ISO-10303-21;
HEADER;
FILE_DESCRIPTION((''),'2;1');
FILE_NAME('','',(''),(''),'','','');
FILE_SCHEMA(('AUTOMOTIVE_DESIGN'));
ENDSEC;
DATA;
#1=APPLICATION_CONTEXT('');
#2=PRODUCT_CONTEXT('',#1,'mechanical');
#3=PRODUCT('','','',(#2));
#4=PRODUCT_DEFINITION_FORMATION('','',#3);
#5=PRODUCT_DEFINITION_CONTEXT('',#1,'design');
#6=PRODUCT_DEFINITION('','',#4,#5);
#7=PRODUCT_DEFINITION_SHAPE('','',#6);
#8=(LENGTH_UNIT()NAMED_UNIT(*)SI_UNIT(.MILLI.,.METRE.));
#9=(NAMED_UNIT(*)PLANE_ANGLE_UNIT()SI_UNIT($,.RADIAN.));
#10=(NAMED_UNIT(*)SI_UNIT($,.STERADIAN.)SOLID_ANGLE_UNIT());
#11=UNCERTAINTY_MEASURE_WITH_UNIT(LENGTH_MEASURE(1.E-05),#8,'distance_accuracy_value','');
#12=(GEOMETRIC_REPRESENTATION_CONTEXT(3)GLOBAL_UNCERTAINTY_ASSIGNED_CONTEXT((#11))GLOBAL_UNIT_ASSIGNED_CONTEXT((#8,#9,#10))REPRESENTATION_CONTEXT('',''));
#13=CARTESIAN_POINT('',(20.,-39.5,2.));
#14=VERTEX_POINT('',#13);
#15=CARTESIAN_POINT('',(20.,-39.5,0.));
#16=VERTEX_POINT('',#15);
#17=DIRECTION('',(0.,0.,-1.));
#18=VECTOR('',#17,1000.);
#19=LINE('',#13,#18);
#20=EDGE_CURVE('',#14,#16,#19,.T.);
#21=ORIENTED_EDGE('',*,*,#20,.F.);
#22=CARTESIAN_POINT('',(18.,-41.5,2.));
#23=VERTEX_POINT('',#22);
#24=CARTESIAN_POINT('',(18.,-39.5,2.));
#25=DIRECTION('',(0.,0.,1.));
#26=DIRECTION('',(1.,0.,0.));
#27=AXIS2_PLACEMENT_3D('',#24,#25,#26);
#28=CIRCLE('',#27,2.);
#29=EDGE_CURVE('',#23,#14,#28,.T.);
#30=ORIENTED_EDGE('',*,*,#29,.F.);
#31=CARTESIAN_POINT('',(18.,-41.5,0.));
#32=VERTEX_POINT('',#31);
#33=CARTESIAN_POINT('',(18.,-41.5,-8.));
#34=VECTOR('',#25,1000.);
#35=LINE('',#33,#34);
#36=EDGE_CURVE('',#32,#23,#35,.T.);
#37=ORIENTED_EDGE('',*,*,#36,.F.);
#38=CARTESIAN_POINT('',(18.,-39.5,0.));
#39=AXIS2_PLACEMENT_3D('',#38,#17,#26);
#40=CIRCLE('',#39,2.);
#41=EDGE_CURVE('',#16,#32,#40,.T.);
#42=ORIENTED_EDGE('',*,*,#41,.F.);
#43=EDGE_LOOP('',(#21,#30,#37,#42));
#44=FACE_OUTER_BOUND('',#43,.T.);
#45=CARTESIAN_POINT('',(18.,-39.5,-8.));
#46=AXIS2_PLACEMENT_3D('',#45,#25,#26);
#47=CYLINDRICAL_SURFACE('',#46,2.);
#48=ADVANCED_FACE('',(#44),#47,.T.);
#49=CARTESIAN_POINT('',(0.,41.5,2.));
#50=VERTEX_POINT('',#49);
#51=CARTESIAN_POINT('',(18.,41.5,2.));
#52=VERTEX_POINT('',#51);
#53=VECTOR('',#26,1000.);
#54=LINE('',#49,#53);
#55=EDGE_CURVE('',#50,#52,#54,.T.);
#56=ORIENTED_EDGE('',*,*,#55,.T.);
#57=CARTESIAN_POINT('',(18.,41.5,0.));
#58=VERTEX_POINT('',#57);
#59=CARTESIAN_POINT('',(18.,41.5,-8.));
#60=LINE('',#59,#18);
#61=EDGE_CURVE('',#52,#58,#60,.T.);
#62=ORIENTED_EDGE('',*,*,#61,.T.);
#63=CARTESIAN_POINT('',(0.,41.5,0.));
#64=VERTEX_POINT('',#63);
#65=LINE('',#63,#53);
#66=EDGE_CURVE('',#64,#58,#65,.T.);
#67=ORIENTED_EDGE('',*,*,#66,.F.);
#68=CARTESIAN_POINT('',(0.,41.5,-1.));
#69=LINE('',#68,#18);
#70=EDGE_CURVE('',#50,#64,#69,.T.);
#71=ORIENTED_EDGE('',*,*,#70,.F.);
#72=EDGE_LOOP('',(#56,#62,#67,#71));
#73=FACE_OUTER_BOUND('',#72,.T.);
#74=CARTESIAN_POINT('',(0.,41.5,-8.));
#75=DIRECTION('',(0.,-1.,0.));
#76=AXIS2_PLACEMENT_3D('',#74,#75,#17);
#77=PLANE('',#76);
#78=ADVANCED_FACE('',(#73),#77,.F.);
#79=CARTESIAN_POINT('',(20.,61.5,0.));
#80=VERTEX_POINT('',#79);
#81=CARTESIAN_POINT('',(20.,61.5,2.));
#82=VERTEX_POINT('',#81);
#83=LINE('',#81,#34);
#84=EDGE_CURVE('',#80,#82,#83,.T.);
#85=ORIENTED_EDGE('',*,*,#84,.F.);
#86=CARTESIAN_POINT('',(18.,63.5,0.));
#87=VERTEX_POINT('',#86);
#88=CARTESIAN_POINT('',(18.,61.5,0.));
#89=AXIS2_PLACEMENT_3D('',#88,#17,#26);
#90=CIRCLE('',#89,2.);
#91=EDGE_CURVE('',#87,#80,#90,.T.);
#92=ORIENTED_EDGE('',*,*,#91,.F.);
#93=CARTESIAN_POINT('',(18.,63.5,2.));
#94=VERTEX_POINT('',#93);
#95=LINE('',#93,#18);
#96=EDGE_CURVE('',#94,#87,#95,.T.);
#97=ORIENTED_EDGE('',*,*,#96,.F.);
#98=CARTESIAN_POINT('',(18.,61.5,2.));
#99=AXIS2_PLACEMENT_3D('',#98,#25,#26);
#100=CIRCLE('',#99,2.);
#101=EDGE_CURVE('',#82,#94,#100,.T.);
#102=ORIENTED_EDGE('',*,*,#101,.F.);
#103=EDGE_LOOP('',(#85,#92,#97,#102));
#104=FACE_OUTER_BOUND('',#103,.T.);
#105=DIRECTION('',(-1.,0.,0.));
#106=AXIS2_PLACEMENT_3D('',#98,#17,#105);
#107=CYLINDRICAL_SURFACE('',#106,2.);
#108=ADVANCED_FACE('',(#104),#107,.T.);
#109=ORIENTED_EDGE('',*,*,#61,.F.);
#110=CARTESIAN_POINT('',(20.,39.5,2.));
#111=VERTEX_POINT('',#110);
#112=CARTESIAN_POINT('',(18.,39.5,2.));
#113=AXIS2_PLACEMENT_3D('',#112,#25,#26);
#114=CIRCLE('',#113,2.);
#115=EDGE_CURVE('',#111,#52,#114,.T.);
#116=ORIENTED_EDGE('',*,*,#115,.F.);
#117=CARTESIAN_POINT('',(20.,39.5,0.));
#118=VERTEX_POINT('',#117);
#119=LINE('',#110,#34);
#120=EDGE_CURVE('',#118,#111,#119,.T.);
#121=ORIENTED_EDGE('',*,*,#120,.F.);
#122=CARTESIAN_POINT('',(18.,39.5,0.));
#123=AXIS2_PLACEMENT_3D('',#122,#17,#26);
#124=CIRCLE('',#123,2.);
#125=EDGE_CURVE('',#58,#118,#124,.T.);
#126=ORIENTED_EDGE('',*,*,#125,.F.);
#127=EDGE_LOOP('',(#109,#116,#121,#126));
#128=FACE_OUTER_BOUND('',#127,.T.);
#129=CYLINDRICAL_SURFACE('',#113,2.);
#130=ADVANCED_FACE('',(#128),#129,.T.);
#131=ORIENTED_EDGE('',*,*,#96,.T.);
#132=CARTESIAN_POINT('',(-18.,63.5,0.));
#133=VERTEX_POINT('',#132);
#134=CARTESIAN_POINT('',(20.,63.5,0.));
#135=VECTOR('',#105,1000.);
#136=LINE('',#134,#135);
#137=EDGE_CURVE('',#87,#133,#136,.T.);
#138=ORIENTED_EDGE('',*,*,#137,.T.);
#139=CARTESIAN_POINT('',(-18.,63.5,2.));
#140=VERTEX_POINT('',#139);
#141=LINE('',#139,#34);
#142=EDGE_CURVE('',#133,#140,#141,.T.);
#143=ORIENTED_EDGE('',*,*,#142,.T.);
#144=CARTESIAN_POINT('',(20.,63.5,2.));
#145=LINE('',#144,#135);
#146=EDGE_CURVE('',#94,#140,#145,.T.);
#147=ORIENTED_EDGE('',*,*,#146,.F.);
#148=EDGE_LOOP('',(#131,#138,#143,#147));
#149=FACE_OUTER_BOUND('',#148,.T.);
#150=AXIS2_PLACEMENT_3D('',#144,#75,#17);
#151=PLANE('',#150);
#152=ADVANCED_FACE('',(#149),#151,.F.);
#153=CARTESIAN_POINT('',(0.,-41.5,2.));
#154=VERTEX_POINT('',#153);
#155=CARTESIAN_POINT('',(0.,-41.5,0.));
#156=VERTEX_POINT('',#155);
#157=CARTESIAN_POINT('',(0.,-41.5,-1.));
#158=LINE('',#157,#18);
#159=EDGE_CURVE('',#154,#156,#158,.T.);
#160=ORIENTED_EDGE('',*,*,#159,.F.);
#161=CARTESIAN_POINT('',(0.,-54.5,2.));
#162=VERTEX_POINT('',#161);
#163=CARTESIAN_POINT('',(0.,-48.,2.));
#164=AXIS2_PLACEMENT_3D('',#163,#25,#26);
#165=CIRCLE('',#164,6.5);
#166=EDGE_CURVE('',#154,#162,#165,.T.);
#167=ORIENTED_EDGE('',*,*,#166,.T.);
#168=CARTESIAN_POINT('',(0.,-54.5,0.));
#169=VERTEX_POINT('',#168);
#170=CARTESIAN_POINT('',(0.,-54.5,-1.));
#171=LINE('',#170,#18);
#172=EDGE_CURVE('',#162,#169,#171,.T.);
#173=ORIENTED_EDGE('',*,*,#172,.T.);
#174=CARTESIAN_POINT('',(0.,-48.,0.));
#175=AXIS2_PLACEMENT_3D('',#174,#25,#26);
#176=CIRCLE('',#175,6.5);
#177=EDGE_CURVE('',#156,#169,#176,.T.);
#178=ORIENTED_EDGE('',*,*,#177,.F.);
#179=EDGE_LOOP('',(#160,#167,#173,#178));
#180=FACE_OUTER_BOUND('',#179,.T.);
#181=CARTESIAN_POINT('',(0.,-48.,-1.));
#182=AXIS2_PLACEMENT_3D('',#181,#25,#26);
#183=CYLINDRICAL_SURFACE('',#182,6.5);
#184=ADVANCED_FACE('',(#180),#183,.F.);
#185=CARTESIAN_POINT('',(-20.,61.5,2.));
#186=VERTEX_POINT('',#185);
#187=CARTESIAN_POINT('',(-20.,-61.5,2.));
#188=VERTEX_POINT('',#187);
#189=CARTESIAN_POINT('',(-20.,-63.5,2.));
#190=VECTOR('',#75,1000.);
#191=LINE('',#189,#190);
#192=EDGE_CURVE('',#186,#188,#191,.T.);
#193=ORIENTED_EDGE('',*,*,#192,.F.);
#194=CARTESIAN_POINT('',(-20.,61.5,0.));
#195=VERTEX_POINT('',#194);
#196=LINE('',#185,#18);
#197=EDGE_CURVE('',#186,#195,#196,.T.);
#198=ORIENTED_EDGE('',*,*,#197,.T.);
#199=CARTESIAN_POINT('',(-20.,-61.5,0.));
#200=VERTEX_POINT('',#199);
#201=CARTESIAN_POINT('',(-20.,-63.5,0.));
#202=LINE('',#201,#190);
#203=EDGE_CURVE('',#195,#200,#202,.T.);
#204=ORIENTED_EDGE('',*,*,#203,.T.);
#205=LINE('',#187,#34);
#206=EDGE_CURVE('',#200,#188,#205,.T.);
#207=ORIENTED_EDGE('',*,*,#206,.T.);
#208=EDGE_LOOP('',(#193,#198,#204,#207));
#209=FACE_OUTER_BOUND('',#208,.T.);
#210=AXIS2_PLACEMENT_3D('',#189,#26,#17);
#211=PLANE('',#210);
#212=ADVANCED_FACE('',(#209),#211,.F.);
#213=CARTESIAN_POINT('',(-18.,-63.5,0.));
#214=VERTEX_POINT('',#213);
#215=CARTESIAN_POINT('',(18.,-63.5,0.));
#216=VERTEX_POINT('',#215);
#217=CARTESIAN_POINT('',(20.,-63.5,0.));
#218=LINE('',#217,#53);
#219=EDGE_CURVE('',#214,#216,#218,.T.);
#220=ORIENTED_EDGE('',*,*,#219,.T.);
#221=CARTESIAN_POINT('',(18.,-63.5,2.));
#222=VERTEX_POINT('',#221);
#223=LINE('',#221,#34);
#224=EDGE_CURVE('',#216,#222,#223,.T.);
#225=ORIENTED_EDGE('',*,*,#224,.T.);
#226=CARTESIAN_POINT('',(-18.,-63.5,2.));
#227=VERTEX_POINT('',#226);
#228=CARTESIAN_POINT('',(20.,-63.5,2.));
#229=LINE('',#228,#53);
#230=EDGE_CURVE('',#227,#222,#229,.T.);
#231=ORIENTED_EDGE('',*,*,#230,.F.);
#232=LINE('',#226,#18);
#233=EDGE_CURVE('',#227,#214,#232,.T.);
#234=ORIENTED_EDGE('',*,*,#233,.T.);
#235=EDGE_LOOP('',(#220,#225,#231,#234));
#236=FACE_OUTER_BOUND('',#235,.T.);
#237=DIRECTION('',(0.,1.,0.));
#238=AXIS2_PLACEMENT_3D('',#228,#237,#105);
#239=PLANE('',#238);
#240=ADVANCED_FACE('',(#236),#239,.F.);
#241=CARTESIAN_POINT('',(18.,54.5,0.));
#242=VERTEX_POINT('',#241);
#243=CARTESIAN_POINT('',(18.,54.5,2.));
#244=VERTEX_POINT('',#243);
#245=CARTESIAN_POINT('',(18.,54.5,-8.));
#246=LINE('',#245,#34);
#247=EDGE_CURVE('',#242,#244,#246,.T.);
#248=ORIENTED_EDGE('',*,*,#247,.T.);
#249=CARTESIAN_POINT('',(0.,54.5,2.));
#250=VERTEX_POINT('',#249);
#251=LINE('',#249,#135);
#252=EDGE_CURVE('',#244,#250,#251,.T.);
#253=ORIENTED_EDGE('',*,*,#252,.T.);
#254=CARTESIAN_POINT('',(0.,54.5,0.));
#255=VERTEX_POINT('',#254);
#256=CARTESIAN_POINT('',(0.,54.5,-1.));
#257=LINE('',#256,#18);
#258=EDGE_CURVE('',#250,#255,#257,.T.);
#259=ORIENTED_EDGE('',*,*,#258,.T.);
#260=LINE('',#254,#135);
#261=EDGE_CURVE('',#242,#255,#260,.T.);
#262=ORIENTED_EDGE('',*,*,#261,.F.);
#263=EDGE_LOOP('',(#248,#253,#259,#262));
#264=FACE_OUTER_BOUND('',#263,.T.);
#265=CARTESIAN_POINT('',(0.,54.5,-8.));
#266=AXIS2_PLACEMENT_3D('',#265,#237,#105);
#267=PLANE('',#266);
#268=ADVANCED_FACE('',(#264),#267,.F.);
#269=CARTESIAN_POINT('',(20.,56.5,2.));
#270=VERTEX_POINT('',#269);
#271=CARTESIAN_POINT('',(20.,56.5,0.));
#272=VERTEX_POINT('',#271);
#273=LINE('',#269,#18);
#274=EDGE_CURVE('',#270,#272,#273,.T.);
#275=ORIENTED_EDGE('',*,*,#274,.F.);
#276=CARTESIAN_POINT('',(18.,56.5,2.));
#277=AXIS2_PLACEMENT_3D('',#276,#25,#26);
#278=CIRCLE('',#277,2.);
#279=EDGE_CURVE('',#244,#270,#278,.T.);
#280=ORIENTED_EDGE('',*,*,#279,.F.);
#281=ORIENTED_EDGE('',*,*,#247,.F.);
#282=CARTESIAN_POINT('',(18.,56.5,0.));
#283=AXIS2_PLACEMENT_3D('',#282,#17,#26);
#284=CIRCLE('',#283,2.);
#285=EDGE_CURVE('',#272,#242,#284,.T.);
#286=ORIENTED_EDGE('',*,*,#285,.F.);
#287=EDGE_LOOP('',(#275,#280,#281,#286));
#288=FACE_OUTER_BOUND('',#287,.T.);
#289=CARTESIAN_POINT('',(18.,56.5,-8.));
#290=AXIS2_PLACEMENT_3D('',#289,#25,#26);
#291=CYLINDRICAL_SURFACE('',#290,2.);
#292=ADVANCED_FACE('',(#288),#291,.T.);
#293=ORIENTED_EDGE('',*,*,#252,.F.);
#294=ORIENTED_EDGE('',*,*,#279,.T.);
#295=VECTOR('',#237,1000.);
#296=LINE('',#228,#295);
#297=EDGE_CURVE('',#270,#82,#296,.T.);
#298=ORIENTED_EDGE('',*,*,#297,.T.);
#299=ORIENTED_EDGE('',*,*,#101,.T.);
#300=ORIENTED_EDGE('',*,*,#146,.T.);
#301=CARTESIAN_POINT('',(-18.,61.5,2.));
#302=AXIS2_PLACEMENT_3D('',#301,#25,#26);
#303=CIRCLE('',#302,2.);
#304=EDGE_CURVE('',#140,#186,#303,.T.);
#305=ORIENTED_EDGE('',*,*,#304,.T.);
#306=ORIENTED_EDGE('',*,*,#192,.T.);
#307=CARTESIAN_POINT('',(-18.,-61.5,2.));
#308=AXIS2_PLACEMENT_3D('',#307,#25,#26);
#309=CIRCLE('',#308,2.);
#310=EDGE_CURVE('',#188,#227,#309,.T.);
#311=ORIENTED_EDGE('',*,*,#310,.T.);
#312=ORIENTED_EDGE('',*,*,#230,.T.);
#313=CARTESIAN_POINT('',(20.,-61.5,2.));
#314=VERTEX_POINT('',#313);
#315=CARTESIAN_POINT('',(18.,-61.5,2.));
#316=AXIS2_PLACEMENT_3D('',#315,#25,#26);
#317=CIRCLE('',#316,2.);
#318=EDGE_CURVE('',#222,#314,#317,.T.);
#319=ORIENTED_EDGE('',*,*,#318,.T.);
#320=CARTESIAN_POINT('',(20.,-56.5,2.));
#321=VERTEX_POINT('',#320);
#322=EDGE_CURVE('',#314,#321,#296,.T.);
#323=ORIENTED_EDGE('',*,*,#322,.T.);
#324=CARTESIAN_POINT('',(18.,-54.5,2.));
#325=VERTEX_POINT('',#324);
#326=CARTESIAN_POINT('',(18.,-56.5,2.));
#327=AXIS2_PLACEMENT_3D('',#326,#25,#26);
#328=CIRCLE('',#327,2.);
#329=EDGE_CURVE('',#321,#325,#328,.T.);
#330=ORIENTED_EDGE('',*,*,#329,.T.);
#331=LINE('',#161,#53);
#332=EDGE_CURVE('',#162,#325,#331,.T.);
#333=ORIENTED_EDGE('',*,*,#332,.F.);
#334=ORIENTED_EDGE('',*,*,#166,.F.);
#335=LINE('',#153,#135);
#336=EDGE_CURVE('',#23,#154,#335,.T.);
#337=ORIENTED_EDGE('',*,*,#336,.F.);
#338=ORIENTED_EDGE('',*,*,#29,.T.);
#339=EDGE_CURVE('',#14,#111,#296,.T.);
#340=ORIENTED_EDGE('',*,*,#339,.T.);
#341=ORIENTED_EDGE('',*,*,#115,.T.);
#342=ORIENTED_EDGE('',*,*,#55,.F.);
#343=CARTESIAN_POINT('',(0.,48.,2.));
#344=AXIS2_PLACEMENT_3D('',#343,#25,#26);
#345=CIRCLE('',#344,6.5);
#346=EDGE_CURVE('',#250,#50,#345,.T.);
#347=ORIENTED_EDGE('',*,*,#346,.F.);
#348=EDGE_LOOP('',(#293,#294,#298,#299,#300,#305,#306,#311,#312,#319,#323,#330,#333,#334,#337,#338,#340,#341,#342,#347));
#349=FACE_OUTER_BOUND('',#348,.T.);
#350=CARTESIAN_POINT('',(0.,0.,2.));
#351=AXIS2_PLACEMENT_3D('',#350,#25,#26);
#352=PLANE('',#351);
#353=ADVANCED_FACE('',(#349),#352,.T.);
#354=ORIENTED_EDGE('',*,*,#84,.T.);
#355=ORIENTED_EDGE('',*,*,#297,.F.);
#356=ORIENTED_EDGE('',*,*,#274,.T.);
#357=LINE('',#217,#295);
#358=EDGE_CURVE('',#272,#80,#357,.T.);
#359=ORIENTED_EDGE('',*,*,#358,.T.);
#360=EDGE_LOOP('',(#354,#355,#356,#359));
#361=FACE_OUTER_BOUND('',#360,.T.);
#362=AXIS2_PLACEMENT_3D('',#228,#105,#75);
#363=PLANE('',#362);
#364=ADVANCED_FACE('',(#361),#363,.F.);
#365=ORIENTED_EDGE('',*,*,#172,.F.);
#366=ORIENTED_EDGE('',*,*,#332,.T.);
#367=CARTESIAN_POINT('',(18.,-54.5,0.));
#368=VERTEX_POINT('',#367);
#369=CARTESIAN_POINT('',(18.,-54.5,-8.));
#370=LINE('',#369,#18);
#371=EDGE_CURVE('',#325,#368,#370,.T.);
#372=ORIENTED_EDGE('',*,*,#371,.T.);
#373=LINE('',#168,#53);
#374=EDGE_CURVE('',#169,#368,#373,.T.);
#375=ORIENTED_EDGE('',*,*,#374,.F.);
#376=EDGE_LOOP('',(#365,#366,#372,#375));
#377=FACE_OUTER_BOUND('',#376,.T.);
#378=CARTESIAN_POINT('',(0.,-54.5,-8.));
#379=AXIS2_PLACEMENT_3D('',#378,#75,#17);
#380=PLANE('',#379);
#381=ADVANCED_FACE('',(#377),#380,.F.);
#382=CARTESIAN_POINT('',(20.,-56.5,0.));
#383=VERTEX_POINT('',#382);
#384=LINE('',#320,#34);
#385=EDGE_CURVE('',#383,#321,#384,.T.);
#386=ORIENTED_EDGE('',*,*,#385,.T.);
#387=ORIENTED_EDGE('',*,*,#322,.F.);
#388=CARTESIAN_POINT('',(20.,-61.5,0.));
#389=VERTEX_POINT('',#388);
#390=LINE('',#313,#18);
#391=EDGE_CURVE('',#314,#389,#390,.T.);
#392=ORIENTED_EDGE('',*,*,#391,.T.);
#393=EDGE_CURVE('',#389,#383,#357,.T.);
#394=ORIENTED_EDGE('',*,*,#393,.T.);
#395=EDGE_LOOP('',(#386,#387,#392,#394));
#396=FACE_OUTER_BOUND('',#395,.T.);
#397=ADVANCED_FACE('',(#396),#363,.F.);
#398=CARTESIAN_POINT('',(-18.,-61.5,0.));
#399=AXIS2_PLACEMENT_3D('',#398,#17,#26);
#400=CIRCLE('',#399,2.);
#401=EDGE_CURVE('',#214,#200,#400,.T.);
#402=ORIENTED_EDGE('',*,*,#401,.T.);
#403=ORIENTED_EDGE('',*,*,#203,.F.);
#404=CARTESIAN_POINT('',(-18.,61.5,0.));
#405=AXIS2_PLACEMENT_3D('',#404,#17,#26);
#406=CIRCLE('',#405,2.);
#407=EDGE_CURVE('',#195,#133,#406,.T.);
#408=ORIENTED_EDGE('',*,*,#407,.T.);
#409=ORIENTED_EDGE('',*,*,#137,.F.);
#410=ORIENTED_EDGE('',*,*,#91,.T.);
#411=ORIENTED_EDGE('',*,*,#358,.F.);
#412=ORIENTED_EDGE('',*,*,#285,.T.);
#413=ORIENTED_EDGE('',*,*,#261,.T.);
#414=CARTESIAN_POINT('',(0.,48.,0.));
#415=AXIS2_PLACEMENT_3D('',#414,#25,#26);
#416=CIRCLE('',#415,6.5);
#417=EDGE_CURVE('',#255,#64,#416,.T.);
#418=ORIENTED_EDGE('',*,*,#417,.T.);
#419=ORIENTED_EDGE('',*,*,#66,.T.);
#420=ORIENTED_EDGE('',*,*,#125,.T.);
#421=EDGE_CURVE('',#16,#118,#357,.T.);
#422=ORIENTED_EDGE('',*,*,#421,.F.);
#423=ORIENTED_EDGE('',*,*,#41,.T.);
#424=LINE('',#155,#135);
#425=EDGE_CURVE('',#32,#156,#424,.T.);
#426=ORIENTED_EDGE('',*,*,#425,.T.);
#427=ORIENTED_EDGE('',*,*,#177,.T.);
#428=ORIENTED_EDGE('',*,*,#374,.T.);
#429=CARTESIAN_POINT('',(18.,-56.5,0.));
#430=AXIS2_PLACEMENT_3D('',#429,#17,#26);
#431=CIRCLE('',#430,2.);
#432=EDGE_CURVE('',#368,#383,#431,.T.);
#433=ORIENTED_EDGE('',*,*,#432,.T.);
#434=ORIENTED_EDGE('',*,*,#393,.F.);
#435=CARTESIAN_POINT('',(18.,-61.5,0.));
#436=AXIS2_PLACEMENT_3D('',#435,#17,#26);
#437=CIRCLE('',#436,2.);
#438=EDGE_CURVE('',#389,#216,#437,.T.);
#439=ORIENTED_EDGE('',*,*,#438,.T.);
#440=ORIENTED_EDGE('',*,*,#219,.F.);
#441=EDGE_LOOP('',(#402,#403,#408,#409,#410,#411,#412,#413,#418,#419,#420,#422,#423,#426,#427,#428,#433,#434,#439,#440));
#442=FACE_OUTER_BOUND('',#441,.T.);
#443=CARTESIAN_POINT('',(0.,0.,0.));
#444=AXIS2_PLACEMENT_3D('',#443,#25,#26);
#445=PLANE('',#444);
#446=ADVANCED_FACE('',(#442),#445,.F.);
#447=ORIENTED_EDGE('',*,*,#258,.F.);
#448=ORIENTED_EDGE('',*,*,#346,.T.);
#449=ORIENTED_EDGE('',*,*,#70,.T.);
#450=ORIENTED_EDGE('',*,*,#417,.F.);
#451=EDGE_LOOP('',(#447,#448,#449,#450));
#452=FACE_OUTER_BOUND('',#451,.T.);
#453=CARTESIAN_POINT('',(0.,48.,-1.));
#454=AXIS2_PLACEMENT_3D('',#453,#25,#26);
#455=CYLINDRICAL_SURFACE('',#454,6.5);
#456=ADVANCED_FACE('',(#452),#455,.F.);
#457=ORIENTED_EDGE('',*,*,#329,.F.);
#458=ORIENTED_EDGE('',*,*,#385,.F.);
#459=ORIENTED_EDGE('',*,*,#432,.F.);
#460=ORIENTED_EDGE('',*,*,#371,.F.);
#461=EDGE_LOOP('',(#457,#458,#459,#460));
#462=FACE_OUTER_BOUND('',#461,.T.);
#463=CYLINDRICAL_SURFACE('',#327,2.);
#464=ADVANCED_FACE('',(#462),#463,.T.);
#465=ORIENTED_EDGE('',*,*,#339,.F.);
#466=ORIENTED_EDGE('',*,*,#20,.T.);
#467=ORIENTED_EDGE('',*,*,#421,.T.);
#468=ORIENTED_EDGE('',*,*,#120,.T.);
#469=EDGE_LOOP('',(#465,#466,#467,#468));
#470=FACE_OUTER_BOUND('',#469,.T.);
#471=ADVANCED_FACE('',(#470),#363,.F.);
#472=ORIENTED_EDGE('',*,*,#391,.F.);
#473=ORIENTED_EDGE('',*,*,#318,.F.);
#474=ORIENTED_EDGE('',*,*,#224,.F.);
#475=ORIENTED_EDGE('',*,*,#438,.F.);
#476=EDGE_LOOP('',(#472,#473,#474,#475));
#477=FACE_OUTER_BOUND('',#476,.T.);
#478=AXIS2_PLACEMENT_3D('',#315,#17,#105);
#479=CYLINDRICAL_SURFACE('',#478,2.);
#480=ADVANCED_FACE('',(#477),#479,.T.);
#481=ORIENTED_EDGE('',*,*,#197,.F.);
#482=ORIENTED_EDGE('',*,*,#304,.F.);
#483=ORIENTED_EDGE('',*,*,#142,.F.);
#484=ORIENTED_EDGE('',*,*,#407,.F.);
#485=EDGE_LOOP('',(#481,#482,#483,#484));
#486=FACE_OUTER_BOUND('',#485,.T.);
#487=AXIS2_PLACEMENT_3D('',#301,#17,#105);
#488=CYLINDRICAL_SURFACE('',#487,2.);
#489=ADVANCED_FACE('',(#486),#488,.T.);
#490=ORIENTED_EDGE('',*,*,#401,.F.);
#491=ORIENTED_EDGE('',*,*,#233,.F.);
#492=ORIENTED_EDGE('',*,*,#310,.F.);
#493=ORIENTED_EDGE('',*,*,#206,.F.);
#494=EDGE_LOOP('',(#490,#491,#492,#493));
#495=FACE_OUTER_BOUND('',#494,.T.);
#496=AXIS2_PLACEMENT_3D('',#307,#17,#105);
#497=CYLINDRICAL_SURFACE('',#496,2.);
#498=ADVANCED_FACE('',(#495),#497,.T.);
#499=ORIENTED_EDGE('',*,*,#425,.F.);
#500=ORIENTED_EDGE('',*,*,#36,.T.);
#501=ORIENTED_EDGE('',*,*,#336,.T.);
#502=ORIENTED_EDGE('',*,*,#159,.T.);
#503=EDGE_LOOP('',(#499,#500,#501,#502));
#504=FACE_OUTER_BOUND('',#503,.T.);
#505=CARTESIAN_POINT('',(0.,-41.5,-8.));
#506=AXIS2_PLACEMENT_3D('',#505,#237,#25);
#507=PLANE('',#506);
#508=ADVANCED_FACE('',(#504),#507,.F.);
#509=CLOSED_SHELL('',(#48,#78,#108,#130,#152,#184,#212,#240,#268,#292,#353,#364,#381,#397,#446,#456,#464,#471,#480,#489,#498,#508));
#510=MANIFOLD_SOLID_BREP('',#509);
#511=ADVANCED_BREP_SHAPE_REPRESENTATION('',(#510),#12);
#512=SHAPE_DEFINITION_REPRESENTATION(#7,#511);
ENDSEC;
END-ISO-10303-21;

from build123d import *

# Parameters (mm, degrees)
SKETCH_1_W          = 40
SKETCH_1_H          = 127
EXTRUDE_1_DEPTH     = 2
SKETCH_2_R          = 6.5
CUT_EXTRUDE_1_DEPTH = 3
SKETCH_4_W          = 20
SKETCH_4_H          = 13
CUT_EXTRUDE_4_DEPTH = 10
FILLET_2_R          = 2


with BuildPart() as part:
    # 草图1 → 凸台-拉伸1 (new body)
    with BuildSketch(Plane.XY):
        Rectangle(SKETCH_1_W, SKETCH_1_H)
    extrude(amount=EXTRUDE_1_DEPTH)

    # 草图2 → 切除-拉伸1 (cut)
    with BuildSketch(Plane.XY.offset(2)):
        with Locations((0, 48)):
            Circle(SKETCH_2_R)
        with Locations((0, -48)):
            Circle(SKETCH_2_R)
    extrude(amount=-CUT_EXTRUDE_1_DEPTH, mode=Mode.SUBTRACT)

    # 草图4 → 切除-拉伸4 (cut)
    with BuildSketch(Plane.XY.offset(2)):
        with Locations((10, 48)):
            Rectangle(SKETCH_4_W, SKETCH_4_H)
        with Locations((10, -48)):
            Rectangle(SKETCH_4_W, SKETCH_4_H)
    extrude(amount=-CUT_EXTRUDE_4_DEPTH, mode=Mode.SUBTRACT)

    # 圆角2
    fillet_2_edges = [part.edges().sort_by_distance(p)[0] for p in [
        (20, 54.5, 1),
        (20, 41.5, 1),
        (20, -41.5, 1),
        (20, -54.5, 1),
        (-20, 63.5, 1),
        (20, 63.5, 1),
        (20, -63.5, 1),
        (-20, -63.5, 1),
    ]]
    fillet(fillet_2_edges, radius=FILLET_2_R)


solid = part.part
